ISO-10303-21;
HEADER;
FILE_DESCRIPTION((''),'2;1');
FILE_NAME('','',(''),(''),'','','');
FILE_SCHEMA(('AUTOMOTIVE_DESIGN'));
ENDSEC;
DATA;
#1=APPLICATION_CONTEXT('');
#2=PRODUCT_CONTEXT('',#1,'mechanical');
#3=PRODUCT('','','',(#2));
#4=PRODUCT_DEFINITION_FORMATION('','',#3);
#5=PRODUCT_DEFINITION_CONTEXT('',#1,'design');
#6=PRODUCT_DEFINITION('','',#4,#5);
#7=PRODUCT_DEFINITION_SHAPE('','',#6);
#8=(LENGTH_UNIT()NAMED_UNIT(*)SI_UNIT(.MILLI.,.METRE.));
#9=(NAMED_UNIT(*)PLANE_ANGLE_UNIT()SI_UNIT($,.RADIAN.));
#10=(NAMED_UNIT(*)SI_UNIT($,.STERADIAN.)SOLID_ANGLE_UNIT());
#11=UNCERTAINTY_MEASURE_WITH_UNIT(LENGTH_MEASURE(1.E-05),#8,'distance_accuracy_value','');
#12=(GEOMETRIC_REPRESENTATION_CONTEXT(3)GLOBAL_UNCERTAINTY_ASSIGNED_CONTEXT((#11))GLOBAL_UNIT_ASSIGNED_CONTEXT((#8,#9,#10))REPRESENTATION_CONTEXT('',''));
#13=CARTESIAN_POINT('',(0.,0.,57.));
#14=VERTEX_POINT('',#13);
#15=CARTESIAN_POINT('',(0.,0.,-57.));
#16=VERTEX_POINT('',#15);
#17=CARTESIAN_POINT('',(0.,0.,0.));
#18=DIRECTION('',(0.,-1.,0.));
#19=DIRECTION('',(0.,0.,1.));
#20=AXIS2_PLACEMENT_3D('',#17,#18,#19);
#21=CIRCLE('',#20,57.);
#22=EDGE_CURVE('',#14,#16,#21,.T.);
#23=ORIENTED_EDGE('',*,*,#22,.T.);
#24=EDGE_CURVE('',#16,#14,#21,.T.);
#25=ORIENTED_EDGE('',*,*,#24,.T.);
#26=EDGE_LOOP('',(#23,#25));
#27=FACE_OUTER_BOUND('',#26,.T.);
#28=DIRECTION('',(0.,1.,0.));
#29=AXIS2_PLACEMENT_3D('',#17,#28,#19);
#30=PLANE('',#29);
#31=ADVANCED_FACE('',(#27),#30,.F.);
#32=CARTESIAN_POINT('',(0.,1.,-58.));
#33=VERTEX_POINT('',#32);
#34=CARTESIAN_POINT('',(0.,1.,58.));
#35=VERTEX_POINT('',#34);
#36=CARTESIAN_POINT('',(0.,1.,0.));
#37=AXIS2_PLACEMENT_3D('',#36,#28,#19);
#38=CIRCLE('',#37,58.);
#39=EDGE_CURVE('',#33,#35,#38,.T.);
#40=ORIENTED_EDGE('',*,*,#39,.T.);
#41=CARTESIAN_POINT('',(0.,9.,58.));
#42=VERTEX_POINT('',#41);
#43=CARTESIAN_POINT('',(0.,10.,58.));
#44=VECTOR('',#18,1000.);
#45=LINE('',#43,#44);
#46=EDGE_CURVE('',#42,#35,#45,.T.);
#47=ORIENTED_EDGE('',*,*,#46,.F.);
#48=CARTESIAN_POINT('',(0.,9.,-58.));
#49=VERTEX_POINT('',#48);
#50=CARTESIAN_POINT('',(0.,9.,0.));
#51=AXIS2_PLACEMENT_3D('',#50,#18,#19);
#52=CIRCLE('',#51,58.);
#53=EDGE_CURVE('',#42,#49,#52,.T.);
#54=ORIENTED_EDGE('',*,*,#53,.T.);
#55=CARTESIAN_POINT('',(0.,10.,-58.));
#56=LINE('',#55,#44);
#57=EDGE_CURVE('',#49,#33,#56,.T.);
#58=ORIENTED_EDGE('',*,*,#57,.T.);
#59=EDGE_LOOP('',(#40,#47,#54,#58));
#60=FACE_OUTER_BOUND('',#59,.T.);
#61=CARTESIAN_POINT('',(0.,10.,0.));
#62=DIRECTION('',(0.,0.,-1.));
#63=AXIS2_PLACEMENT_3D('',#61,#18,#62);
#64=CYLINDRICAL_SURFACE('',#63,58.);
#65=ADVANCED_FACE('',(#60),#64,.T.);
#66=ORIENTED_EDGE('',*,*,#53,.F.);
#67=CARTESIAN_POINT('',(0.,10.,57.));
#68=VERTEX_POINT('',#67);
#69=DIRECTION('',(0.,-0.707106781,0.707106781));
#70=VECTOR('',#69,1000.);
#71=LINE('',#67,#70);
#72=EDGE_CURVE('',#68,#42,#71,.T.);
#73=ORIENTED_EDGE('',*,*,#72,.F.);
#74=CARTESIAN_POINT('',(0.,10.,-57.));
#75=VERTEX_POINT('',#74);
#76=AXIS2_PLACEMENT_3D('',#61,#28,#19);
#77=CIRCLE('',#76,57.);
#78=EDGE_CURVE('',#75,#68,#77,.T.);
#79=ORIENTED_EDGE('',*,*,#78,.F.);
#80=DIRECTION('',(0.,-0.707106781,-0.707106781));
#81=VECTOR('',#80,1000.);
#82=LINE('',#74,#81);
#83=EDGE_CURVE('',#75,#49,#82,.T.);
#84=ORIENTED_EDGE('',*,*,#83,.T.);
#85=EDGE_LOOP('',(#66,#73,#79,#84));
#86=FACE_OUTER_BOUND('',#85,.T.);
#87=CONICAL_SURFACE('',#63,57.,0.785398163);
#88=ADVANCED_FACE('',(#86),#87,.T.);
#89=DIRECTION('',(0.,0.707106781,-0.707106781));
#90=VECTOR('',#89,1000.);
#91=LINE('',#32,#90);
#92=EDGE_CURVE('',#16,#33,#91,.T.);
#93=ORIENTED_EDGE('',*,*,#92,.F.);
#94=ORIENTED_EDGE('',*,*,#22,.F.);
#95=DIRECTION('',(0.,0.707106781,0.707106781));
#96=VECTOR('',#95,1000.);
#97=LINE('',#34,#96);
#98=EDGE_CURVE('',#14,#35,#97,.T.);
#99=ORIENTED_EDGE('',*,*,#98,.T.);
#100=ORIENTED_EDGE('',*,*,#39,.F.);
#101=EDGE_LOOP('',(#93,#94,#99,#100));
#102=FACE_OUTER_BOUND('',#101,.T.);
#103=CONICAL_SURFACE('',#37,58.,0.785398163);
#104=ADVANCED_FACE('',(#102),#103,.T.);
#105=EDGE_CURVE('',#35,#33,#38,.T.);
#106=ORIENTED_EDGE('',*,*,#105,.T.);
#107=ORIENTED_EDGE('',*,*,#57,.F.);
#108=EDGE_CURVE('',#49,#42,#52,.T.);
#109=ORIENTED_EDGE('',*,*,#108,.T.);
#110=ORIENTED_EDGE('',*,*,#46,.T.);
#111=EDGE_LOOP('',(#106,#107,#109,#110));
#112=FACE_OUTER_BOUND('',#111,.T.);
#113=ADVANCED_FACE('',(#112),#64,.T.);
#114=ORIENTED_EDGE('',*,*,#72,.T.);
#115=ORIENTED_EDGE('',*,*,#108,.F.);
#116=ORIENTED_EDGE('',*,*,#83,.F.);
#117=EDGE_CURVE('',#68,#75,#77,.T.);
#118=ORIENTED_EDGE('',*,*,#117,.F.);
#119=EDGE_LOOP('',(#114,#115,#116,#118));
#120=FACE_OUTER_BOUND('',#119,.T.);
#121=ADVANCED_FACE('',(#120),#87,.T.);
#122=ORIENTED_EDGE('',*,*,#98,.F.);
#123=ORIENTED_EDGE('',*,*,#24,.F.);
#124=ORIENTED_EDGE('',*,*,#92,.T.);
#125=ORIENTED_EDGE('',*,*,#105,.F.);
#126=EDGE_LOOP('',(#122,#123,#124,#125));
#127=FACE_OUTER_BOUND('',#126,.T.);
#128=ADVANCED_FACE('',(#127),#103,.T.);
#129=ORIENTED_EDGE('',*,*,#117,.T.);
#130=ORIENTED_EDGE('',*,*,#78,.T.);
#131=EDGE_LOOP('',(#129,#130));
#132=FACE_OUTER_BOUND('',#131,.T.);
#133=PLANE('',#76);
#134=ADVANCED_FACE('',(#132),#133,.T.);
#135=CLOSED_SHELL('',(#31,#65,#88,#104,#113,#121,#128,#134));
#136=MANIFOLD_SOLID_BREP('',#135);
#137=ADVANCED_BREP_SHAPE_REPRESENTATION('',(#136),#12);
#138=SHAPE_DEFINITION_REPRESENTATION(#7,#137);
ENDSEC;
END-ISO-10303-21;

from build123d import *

# Parameters (mm, degrees)
SKETCH1_R           = 58
BOSS_EXTRUDE1_DEPTH = 10
CHAMFER1_SIZE       = 1


with BuildPart() as part:
    # Sketch1 → Boss-Extrude1 (new body)
    with BuildSketch(Plane(origin=(0, 0, 0), x_dir=(1, 0, 0), z_dir=(0, 1, 0))):
        with Locations(Location((0, 0, 0), (0, 0, 270))):
            Circle(SKETCH1_R)
    extrude(amount=BOSS_EXTRUDE1_DEPTH)

    # Chamfer1
    chamfer1_edges = [part.edges().sort_by_distance(p)[0] for p in [
        (0, 0, -58),
        (0, 10, -58),
    ]]
    chamfer(chamfer1_edges, length=CHAMFER1_SIZE)


solid = part.part
